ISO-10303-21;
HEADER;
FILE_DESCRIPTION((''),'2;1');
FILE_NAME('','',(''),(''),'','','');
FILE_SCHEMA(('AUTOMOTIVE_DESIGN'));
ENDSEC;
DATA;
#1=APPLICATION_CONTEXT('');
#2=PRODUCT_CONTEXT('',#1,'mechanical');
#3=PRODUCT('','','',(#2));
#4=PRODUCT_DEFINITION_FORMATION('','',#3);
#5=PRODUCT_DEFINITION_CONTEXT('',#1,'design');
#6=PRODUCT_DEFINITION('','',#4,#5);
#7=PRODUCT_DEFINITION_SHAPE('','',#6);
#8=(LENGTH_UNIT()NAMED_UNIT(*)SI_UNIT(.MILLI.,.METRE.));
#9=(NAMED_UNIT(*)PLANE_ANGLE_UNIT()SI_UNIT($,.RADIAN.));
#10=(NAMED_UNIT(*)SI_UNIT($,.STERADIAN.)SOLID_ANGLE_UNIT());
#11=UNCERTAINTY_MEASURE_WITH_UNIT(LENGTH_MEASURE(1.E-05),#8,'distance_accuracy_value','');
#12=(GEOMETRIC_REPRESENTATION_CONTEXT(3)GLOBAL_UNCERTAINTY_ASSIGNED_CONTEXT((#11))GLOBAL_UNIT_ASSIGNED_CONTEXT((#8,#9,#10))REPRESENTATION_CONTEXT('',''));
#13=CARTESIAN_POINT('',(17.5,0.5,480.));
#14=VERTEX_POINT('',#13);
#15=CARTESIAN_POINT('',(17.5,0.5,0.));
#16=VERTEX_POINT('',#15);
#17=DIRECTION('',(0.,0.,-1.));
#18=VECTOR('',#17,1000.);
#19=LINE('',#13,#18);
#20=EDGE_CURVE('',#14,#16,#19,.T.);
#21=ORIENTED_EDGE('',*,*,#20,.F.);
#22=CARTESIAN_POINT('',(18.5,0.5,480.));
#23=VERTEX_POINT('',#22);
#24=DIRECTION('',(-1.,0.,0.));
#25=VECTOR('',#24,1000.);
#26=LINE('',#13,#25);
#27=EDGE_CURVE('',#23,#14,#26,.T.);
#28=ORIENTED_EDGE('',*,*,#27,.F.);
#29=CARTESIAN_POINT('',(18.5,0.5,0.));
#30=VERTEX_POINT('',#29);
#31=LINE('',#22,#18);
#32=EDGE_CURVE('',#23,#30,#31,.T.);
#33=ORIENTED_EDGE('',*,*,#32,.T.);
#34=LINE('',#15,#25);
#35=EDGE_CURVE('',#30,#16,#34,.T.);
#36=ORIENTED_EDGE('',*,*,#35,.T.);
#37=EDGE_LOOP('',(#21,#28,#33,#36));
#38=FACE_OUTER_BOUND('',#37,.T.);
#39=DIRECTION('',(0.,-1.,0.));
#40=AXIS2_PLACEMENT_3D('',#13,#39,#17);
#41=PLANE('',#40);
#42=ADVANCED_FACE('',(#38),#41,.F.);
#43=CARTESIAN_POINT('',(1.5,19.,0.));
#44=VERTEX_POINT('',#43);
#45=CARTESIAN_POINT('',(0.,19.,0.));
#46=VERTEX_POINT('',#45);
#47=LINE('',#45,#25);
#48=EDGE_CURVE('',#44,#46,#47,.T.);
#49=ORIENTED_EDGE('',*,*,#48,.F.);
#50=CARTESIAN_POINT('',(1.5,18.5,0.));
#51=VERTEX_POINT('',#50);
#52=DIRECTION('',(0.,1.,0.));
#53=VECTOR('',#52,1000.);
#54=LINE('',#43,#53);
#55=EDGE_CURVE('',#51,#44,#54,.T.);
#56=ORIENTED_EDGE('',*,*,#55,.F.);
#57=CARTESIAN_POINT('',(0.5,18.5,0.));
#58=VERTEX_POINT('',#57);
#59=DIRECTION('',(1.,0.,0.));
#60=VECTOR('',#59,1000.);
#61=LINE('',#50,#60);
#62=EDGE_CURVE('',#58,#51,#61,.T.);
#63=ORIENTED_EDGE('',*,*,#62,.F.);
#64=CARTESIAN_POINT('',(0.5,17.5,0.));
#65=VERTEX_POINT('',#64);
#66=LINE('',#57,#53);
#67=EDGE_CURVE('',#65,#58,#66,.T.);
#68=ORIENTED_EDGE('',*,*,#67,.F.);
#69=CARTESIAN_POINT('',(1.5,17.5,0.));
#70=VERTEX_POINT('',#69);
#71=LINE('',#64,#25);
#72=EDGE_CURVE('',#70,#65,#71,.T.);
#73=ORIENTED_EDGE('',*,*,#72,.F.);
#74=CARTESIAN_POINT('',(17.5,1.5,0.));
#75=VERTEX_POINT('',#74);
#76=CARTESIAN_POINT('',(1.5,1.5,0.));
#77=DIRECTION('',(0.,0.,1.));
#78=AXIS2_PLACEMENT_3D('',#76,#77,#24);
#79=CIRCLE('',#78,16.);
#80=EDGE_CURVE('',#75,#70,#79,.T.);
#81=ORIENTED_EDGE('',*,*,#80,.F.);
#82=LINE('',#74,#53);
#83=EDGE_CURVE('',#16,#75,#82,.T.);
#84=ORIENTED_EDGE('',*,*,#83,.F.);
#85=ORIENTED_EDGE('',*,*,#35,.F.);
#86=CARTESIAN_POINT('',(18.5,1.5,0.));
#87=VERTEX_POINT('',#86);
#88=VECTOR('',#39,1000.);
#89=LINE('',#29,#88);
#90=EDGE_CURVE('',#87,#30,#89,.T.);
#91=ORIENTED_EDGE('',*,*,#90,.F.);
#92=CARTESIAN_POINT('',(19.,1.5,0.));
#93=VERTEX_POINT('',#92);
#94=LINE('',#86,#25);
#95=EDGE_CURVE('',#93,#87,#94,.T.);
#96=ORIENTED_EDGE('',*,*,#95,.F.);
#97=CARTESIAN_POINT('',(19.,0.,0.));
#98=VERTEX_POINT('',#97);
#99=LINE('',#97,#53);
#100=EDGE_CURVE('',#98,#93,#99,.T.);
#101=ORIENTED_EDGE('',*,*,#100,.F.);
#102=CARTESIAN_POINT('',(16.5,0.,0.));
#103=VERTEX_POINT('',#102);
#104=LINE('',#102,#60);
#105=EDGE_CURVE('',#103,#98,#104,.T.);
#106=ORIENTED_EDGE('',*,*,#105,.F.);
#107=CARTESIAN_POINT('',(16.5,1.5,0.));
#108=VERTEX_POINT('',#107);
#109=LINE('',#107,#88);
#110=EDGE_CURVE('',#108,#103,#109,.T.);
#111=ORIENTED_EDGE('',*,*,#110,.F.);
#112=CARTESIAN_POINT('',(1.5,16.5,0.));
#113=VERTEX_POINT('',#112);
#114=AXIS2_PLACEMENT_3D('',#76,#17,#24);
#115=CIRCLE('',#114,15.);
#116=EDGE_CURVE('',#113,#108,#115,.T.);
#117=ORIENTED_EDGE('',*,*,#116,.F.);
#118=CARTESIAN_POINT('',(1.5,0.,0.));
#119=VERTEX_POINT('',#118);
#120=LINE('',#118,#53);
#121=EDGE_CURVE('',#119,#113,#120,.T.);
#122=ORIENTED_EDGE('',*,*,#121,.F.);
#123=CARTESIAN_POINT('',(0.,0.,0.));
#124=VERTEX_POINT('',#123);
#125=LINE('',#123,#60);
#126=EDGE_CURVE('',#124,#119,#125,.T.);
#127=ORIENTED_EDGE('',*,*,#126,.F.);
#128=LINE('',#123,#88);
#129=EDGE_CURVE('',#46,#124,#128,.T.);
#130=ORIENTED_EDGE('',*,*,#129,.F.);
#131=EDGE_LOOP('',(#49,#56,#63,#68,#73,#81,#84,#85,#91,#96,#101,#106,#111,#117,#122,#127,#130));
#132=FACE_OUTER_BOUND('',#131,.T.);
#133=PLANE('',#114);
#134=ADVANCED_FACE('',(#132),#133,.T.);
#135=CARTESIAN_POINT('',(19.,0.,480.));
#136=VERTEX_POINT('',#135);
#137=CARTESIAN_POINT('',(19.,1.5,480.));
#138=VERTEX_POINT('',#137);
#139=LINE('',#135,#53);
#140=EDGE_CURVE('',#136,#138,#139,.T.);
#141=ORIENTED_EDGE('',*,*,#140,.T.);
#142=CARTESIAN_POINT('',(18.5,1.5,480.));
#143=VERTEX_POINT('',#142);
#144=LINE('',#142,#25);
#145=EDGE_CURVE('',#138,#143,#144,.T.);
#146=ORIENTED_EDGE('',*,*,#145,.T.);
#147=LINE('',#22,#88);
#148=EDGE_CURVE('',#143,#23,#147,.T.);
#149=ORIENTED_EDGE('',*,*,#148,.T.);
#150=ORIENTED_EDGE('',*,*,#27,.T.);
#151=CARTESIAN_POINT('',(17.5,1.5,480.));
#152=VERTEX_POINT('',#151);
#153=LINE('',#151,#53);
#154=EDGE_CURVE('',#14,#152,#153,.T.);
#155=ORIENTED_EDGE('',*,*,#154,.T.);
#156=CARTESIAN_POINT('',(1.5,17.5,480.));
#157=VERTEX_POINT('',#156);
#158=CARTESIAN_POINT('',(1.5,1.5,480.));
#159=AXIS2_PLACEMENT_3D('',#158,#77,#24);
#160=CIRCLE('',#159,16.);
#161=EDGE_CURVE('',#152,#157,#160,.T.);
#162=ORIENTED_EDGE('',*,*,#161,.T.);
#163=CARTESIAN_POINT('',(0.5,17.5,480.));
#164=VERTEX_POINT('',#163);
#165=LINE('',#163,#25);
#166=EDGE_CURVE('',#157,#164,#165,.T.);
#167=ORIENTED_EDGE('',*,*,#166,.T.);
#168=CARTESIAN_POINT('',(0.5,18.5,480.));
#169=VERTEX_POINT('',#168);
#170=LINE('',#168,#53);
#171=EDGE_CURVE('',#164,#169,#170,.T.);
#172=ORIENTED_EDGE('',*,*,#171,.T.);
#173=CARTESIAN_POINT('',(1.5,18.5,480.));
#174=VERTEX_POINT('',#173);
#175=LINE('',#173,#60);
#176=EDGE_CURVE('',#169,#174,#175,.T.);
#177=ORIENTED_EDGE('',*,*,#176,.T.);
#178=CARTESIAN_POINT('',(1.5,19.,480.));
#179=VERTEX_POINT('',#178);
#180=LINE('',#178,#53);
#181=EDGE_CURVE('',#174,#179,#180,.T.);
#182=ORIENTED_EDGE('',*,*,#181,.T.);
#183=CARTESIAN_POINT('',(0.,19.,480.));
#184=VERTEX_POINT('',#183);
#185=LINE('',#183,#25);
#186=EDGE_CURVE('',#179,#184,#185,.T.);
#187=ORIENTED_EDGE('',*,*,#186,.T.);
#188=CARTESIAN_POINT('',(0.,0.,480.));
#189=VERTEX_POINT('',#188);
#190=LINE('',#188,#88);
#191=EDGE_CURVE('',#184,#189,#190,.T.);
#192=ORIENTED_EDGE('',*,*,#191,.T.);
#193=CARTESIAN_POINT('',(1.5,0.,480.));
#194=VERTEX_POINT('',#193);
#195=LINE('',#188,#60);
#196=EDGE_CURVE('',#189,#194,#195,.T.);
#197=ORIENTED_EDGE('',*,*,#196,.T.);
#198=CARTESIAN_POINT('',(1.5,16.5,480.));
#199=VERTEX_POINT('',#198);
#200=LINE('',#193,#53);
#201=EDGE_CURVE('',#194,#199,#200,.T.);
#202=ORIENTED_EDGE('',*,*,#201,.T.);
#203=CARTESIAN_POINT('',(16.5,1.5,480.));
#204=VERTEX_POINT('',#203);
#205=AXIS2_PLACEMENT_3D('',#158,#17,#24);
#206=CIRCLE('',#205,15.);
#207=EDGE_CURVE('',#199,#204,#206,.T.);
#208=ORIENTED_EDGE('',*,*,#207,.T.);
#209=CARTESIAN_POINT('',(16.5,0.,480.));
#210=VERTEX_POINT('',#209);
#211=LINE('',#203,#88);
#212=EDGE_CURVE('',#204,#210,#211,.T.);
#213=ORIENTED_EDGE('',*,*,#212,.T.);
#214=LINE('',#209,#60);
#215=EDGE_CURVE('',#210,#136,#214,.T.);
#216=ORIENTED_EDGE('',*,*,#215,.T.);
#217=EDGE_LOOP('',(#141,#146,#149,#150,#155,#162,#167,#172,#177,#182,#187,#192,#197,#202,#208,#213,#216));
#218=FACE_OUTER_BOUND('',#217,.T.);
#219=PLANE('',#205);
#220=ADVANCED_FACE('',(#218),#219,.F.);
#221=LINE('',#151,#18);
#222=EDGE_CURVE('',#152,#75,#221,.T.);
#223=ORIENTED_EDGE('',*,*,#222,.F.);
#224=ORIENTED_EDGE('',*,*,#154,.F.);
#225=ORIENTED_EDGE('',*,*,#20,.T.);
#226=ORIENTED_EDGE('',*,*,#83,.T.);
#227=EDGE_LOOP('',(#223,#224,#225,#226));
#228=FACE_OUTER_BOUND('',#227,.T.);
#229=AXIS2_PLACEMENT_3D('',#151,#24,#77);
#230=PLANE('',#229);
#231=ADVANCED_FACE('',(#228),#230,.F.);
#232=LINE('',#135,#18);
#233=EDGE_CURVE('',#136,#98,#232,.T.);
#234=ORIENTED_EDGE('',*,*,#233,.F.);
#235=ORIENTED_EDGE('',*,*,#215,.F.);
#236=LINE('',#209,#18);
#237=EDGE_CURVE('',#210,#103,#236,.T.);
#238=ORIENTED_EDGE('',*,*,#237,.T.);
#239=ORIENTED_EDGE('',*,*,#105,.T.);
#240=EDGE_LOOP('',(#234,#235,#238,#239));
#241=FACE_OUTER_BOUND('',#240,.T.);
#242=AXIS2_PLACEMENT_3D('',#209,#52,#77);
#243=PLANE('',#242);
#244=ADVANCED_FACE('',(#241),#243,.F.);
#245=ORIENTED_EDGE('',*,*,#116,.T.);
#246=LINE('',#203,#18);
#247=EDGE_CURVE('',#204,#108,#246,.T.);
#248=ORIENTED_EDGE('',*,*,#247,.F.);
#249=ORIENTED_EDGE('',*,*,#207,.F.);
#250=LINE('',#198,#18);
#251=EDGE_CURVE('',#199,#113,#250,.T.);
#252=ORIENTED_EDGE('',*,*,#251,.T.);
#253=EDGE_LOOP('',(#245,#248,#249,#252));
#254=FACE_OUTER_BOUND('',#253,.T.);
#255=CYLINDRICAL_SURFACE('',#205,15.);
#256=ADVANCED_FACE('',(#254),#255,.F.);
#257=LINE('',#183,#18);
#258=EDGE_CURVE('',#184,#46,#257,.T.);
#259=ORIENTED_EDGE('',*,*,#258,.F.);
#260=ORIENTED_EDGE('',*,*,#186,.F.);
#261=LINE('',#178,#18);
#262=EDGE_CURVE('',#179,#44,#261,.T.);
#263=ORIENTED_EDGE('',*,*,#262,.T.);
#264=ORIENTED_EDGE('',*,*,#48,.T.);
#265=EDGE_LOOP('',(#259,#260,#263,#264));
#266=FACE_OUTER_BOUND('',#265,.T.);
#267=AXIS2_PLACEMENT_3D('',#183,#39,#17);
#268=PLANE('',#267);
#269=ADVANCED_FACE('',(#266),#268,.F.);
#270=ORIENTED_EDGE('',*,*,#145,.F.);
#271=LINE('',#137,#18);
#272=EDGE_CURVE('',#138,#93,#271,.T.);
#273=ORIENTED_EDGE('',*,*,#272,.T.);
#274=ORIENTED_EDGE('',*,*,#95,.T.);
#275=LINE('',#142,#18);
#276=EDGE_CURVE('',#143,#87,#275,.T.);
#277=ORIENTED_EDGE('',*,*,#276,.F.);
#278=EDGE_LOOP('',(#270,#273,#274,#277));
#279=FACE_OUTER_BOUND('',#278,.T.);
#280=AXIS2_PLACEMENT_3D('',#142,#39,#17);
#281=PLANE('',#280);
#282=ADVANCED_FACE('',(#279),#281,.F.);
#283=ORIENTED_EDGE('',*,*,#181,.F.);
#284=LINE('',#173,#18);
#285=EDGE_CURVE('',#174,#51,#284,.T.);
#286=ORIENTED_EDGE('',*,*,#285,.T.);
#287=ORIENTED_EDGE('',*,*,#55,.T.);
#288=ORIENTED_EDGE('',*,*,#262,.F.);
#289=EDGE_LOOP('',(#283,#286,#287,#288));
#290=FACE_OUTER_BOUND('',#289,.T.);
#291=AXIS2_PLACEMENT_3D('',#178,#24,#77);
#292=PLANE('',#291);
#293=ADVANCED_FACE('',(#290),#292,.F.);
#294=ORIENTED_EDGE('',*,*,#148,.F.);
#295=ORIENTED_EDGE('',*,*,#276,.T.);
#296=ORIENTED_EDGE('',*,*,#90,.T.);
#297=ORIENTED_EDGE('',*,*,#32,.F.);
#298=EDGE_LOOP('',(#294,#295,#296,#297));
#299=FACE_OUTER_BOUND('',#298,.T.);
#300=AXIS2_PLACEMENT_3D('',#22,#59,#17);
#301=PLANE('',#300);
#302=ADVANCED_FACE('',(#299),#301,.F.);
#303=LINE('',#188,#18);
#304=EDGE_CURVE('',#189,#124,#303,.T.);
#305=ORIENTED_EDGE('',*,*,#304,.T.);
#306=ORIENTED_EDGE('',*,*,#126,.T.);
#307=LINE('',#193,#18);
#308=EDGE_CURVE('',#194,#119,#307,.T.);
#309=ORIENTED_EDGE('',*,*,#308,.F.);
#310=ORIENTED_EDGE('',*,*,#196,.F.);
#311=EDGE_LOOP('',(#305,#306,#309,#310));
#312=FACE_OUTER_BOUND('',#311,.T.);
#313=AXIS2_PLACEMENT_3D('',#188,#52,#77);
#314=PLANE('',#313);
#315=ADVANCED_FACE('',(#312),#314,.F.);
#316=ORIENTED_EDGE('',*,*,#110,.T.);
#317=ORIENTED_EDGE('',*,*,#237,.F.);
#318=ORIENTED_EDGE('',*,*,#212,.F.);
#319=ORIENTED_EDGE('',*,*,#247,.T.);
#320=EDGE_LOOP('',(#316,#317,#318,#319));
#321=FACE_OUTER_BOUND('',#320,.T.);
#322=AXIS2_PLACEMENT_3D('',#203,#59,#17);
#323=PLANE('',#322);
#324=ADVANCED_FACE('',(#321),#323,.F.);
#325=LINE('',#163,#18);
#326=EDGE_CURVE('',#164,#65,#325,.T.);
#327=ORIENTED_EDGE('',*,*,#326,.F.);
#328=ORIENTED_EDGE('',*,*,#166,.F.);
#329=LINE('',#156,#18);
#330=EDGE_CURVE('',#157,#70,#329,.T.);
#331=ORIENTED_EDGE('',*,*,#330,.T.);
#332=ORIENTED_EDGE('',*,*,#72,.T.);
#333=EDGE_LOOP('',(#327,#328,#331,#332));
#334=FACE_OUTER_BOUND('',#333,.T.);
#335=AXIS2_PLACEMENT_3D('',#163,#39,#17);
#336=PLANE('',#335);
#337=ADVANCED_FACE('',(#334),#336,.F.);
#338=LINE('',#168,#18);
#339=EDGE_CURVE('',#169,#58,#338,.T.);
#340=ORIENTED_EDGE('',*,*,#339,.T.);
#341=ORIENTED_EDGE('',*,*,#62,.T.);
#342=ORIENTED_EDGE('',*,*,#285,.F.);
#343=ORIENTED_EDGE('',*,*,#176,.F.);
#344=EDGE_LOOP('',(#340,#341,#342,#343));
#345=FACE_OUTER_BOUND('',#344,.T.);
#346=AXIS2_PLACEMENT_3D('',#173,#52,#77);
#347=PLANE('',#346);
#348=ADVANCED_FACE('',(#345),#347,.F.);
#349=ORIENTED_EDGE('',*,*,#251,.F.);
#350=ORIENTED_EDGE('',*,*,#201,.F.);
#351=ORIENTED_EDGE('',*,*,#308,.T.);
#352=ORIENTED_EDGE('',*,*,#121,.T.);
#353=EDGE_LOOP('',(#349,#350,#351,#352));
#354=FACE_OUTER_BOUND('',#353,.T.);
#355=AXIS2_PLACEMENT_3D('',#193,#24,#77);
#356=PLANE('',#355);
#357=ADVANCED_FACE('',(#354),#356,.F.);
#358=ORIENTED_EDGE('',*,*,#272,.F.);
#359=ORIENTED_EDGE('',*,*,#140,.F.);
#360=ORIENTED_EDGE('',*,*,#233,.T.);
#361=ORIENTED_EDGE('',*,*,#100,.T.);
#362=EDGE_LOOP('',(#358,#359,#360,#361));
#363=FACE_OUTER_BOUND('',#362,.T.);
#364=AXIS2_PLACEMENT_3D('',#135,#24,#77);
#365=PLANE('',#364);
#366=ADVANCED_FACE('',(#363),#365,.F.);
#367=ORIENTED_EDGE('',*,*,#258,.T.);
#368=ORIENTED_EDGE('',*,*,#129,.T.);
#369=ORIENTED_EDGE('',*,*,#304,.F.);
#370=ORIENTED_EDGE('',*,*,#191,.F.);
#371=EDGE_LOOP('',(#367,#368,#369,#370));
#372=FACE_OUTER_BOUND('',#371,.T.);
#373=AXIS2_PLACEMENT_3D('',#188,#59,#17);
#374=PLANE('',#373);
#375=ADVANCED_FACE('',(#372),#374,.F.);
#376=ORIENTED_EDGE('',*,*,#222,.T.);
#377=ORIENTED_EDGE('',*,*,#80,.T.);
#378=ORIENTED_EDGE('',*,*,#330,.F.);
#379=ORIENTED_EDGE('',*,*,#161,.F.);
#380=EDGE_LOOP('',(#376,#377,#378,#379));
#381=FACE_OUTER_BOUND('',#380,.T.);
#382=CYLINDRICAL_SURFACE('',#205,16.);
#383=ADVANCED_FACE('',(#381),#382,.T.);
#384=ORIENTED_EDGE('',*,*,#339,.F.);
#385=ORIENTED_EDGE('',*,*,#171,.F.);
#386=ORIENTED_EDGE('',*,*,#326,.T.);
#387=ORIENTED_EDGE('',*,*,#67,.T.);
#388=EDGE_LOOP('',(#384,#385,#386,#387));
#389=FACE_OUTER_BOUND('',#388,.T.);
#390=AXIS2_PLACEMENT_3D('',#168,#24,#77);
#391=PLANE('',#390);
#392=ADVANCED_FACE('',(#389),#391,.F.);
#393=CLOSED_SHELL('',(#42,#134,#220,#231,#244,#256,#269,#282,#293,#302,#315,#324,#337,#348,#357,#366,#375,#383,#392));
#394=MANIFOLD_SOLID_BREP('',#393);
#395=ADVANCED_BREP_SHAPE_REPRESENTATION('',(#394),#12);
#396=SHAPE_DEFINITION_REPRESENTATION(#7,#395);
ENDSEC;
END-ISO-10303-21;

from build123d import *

# Parameters (mm, degrees)
BOSS_EXTRUDE1_DEPTH = 480


with BuildPart() as part:
    # Sketch1 → Boss-Extrude1 (new body)
    with BuildSketch(Plane.XY):
        with BuildLine():
            Line((0, 0), (0, 19))
            Line((0, 19), (1.5, 19))
            Line((1.5, 19), (1.5, 18.5))
            Line((1.5, 18.5), (0.5, 18.5))
            Line((0.5, 18.5), (0.5, 17.5))
            Line((0.5, 17.5), (1.5, 17.5))
            ThreePointArc((1.5, 17.5), (12.813708499, 12.813708499), (17.5, 1.5))
            Line((17.5, 1.5), (17.5, 0.5))
            Line((17.5, 0.5), (18.5, 0.5))
            Line((18.5, 0.5), (18.5, 1.5))
            Line((18.5, 1.5), (19, 1.5))
            Line((19, 1.5), (19, 0))
            Line((19, 0), (16.5, 0))
            Line((16.5, 0), (16.5, 1.5))
            ThreePointArc((16.5, 1.5), (12.106601718, 12.106601718), (1.5, 16.5))
            Line((1.5, 16.5), (1.5, 0))
            Line((1.5, 0), (0, 0))
        make_face()
    extrude(amount=BOSS_EXTRUDE1_DEPTH)


solid = part.part
